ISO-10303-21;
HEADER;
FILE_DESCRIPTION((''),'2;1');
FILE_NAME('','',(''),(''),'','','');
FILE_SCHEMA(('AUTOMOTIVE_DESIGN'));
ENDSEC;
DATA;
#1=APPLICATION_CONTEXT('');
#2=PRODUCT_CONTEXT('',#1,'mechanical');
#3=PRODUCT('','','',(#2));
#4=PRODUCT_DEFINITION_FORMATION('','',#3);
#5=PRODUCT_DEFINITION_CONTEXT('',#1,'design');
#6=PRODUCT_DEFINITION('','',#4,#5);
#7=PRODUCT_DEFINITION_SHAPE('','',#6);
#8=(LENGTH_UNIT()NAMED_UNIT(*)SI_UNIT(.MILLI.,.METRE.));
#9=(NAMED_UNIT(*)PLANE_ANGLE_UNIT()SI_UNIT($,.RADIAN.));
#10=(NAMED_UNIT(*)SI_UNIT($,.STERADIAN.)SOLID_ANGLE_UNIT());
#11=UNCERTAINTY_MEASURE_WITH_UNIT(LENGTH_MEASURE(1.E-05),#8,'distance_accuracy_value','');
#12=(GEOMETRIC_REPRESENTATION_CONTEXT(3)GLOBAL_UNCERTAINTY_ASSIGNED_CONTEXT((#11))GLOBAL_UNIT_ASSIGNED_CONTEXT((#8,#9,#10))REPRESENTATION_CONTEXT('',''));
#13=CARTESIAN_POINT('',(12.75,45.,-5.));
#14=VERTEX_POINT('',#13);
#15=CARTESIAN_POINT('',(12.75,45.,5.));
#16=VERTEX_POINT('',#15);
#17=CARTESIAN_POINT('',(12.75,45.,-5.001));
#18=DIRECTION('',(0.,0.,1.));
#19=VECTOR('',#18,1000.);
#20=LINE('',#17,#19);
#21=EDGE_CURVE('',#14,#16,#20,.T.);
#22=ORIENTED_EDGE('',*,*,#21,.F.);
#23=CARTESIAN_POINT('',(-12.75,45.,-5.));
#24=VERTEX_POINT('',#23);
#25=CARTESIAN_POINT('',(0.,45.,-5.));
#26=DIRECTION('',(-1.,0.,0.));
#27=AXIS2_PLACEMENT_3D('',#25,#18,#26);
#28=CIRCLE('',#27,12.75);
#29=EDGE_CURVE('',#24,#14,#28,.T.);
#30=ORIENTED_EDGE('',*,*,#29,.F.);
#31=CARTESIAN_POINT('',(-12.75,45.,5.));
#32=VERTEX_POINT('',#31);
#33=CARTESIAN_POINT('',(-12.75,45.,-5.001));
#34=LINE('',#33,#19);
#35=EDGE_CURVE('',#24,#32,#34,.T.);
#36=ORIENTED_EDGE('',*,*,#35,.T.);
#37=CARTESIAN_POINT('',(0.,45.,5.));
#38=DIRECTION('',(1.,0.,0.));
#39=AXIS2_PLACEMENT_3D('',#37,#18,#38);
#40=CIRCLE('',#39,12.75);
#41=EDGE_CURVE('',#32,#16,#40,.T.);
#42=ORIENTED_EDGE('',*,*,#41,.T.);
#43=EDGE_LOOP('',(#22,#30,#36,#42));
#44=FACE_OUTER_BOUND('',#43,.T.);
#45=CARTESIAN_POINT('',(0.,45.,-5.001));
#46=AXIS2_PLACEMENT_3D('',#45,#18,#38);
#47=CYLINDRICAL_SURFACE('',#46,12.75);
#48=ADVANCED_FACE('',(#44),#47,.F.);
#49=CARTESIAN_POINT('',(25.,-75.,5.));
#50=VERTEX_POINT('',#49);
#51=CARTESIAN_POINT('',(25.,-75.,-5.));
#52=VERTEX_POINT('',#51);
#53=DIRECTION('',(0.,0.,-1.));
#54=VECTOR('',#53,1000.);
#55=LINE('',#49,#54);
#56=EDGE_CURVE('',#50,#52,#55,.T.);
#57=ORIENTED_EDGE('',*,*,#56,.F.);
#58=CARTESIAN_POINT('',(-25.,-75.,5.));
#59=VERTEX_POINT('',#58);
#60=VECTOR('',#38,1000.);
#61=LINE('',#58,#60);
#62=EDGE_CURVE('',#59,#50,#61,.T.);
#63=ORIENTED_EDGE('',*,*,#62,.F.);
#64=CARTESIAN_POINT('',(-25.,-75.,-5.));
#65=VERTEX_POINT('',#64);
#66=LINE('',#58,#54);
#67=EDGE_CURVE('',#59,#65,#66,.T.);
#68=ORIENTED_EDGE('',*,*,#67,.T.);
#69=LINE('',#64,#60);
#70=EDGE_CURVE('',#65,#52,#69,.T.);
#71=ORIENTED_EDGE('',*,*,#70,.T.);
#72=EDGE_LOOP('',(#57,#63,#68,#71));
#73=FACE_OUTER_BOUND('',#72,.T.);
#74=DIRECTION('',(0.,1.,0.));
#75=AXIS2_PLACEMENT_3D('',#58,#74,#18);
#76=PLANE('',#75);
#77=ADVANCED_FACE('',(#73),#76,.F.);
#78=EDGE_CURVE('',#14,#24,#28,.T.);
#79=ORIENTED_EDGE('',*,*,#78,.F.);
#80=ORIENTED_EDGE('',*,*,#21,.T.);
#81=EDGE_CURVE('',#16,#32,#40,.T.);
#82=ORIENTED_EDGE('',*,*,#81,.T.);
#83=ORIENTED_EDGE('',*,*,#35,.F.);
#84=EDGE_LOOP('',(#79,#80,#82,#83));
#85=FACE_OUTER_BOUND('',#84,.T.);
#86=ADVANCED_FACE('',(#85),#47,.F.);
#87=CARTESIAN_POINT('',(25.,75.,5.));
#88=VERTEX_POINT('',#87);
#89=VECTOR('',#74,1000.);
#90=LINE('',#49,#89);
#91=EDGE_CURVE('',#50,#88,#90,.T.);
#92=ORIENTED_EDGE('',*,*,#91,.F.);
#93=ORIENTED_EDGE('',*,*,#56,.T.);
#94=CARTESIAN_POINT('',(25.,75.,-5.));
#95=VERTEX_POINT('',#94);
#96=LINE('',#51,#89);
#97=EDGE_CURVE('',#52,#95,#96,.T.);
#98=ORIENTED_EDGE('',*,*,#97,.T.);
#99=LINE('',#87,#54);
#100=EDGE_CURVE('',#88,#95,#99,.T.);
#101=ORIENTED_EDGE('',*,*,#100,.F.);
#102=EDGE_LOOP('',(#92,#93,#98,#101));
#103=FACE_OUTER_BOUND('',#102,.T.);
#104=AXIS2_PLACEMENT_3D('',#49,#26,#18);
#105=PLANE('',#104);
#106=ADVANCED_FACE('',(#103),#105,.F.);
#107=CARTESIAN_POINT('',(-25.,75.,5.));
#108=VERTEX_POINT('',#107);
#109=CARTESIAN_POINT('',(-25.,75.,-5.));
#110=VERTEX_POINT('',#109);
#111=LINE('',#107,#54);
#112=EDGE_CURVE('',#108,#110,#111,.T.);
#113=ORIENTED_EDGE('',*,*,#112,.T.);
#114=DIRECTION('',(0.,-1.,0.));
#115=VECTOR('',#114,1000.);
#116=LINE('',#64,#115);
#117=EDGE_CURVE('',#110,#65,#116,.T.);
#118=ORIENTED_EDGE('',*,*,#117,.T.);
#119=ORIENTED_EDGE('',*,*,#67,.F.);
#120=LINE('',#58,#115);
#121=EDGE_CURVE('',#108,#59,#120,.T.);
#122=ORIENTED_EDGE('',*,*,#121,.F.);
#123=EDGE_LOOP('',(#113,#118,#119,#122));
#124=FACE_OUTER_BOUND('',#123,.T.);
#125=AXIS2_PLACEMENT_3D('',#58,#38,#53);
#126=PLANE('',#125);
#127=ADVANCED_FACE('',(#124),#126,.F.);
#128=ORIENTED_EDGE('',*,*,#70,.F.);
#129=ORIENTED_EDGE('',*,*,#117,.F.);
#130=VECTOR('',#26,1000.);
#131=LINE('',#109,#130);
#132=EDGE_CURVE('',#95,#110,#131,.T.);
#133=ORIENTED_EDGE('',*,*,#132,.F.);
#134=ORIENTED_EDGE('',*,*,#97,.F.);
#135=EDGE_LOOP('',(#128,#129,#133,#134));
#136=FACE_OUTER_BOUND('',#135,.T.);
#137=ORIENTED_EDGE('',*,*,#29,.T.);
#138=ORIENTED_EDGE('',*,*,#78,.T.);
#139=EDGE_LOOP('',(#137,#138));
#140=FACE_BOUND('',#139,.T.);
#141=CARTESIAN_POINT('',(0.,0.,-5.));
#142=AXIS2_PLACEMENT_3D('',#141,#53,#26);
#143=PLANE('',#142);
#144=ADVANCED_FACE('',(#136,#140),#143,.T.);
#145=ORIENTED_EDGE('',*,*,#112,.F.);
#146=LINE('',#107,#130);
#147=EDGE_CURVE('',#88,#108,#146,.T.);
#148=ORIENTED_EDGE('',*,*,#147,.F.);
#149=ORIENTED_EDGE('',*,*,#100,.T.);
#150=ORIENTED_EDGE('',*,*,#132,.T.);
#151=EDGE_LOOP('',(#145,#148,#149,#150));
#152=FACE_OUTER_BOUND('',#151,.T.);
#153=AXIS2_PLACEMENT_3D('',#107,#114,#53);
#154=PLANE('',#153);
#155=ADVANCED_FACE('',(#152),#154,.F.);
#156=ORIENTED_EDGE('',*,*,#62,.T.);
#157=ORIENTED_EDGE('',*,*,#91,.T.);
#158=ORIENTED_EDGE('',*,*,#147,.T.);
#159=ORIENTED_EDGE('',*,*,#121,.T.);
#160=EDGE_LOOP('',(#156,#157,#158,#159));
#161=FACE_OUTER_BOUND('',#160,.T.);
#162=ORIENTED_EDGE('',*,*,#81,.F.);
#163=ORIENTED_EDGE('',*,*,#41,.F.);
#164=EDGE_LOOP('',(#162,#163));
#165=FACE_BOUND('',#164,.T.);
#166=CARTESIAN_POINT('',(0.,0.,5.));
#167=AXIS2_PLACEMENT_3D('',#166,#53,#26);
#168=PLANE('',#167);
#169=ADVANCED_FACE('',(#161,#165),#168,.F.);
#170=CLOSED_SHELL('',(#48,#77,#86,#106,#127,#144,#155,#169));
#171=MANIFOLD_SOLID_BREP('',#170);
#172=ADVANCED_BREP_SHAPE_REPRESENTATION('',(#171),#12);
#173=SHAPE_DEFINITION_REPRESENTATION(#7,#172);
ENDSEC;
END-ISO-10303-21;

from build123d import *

# Parameters (mm, degrees)
SKETCH_1_W          = 50
SKETCH_1_H          = 150
EXTRUDE_1_DEPTH     = 5
CUT_EXTRUDE_1_REACH = 81.687
SKETCH_2_R          = 12.75


with BuildPart() as part:
    # 草图1 → 凸台-拉伸1 (new, symmetric)
    with BuildSketch(Plane.XY):
        Rectangle(SKETCH_1_W, SKETCH_1_H)
    extrude(amount=EXTRUDE_1_DEPTH, both=True)

    # 草图2 → 切除-拉伸1 (cut, up to next)
    with BuildSketch(Plane.XY.offset(5), mode=Mode.PRIVATE) as cut_extrude_1_sk1:
        with Locations((0, 45)):
            Circle(SKETCH_2_R)
    cut_extrude_1_tool1 = extrude(cut_extrude_1_sk1.sketch, amount=-CUT_EXTRUDE_1_REACH, mode=Mode.PRIVATE) & part.part
    add(cut_extrude_1_tool1.solids().sort_by_distance((0, 45, 5))[0], mode=Mode.SUBTRACT)


solid = part.part
